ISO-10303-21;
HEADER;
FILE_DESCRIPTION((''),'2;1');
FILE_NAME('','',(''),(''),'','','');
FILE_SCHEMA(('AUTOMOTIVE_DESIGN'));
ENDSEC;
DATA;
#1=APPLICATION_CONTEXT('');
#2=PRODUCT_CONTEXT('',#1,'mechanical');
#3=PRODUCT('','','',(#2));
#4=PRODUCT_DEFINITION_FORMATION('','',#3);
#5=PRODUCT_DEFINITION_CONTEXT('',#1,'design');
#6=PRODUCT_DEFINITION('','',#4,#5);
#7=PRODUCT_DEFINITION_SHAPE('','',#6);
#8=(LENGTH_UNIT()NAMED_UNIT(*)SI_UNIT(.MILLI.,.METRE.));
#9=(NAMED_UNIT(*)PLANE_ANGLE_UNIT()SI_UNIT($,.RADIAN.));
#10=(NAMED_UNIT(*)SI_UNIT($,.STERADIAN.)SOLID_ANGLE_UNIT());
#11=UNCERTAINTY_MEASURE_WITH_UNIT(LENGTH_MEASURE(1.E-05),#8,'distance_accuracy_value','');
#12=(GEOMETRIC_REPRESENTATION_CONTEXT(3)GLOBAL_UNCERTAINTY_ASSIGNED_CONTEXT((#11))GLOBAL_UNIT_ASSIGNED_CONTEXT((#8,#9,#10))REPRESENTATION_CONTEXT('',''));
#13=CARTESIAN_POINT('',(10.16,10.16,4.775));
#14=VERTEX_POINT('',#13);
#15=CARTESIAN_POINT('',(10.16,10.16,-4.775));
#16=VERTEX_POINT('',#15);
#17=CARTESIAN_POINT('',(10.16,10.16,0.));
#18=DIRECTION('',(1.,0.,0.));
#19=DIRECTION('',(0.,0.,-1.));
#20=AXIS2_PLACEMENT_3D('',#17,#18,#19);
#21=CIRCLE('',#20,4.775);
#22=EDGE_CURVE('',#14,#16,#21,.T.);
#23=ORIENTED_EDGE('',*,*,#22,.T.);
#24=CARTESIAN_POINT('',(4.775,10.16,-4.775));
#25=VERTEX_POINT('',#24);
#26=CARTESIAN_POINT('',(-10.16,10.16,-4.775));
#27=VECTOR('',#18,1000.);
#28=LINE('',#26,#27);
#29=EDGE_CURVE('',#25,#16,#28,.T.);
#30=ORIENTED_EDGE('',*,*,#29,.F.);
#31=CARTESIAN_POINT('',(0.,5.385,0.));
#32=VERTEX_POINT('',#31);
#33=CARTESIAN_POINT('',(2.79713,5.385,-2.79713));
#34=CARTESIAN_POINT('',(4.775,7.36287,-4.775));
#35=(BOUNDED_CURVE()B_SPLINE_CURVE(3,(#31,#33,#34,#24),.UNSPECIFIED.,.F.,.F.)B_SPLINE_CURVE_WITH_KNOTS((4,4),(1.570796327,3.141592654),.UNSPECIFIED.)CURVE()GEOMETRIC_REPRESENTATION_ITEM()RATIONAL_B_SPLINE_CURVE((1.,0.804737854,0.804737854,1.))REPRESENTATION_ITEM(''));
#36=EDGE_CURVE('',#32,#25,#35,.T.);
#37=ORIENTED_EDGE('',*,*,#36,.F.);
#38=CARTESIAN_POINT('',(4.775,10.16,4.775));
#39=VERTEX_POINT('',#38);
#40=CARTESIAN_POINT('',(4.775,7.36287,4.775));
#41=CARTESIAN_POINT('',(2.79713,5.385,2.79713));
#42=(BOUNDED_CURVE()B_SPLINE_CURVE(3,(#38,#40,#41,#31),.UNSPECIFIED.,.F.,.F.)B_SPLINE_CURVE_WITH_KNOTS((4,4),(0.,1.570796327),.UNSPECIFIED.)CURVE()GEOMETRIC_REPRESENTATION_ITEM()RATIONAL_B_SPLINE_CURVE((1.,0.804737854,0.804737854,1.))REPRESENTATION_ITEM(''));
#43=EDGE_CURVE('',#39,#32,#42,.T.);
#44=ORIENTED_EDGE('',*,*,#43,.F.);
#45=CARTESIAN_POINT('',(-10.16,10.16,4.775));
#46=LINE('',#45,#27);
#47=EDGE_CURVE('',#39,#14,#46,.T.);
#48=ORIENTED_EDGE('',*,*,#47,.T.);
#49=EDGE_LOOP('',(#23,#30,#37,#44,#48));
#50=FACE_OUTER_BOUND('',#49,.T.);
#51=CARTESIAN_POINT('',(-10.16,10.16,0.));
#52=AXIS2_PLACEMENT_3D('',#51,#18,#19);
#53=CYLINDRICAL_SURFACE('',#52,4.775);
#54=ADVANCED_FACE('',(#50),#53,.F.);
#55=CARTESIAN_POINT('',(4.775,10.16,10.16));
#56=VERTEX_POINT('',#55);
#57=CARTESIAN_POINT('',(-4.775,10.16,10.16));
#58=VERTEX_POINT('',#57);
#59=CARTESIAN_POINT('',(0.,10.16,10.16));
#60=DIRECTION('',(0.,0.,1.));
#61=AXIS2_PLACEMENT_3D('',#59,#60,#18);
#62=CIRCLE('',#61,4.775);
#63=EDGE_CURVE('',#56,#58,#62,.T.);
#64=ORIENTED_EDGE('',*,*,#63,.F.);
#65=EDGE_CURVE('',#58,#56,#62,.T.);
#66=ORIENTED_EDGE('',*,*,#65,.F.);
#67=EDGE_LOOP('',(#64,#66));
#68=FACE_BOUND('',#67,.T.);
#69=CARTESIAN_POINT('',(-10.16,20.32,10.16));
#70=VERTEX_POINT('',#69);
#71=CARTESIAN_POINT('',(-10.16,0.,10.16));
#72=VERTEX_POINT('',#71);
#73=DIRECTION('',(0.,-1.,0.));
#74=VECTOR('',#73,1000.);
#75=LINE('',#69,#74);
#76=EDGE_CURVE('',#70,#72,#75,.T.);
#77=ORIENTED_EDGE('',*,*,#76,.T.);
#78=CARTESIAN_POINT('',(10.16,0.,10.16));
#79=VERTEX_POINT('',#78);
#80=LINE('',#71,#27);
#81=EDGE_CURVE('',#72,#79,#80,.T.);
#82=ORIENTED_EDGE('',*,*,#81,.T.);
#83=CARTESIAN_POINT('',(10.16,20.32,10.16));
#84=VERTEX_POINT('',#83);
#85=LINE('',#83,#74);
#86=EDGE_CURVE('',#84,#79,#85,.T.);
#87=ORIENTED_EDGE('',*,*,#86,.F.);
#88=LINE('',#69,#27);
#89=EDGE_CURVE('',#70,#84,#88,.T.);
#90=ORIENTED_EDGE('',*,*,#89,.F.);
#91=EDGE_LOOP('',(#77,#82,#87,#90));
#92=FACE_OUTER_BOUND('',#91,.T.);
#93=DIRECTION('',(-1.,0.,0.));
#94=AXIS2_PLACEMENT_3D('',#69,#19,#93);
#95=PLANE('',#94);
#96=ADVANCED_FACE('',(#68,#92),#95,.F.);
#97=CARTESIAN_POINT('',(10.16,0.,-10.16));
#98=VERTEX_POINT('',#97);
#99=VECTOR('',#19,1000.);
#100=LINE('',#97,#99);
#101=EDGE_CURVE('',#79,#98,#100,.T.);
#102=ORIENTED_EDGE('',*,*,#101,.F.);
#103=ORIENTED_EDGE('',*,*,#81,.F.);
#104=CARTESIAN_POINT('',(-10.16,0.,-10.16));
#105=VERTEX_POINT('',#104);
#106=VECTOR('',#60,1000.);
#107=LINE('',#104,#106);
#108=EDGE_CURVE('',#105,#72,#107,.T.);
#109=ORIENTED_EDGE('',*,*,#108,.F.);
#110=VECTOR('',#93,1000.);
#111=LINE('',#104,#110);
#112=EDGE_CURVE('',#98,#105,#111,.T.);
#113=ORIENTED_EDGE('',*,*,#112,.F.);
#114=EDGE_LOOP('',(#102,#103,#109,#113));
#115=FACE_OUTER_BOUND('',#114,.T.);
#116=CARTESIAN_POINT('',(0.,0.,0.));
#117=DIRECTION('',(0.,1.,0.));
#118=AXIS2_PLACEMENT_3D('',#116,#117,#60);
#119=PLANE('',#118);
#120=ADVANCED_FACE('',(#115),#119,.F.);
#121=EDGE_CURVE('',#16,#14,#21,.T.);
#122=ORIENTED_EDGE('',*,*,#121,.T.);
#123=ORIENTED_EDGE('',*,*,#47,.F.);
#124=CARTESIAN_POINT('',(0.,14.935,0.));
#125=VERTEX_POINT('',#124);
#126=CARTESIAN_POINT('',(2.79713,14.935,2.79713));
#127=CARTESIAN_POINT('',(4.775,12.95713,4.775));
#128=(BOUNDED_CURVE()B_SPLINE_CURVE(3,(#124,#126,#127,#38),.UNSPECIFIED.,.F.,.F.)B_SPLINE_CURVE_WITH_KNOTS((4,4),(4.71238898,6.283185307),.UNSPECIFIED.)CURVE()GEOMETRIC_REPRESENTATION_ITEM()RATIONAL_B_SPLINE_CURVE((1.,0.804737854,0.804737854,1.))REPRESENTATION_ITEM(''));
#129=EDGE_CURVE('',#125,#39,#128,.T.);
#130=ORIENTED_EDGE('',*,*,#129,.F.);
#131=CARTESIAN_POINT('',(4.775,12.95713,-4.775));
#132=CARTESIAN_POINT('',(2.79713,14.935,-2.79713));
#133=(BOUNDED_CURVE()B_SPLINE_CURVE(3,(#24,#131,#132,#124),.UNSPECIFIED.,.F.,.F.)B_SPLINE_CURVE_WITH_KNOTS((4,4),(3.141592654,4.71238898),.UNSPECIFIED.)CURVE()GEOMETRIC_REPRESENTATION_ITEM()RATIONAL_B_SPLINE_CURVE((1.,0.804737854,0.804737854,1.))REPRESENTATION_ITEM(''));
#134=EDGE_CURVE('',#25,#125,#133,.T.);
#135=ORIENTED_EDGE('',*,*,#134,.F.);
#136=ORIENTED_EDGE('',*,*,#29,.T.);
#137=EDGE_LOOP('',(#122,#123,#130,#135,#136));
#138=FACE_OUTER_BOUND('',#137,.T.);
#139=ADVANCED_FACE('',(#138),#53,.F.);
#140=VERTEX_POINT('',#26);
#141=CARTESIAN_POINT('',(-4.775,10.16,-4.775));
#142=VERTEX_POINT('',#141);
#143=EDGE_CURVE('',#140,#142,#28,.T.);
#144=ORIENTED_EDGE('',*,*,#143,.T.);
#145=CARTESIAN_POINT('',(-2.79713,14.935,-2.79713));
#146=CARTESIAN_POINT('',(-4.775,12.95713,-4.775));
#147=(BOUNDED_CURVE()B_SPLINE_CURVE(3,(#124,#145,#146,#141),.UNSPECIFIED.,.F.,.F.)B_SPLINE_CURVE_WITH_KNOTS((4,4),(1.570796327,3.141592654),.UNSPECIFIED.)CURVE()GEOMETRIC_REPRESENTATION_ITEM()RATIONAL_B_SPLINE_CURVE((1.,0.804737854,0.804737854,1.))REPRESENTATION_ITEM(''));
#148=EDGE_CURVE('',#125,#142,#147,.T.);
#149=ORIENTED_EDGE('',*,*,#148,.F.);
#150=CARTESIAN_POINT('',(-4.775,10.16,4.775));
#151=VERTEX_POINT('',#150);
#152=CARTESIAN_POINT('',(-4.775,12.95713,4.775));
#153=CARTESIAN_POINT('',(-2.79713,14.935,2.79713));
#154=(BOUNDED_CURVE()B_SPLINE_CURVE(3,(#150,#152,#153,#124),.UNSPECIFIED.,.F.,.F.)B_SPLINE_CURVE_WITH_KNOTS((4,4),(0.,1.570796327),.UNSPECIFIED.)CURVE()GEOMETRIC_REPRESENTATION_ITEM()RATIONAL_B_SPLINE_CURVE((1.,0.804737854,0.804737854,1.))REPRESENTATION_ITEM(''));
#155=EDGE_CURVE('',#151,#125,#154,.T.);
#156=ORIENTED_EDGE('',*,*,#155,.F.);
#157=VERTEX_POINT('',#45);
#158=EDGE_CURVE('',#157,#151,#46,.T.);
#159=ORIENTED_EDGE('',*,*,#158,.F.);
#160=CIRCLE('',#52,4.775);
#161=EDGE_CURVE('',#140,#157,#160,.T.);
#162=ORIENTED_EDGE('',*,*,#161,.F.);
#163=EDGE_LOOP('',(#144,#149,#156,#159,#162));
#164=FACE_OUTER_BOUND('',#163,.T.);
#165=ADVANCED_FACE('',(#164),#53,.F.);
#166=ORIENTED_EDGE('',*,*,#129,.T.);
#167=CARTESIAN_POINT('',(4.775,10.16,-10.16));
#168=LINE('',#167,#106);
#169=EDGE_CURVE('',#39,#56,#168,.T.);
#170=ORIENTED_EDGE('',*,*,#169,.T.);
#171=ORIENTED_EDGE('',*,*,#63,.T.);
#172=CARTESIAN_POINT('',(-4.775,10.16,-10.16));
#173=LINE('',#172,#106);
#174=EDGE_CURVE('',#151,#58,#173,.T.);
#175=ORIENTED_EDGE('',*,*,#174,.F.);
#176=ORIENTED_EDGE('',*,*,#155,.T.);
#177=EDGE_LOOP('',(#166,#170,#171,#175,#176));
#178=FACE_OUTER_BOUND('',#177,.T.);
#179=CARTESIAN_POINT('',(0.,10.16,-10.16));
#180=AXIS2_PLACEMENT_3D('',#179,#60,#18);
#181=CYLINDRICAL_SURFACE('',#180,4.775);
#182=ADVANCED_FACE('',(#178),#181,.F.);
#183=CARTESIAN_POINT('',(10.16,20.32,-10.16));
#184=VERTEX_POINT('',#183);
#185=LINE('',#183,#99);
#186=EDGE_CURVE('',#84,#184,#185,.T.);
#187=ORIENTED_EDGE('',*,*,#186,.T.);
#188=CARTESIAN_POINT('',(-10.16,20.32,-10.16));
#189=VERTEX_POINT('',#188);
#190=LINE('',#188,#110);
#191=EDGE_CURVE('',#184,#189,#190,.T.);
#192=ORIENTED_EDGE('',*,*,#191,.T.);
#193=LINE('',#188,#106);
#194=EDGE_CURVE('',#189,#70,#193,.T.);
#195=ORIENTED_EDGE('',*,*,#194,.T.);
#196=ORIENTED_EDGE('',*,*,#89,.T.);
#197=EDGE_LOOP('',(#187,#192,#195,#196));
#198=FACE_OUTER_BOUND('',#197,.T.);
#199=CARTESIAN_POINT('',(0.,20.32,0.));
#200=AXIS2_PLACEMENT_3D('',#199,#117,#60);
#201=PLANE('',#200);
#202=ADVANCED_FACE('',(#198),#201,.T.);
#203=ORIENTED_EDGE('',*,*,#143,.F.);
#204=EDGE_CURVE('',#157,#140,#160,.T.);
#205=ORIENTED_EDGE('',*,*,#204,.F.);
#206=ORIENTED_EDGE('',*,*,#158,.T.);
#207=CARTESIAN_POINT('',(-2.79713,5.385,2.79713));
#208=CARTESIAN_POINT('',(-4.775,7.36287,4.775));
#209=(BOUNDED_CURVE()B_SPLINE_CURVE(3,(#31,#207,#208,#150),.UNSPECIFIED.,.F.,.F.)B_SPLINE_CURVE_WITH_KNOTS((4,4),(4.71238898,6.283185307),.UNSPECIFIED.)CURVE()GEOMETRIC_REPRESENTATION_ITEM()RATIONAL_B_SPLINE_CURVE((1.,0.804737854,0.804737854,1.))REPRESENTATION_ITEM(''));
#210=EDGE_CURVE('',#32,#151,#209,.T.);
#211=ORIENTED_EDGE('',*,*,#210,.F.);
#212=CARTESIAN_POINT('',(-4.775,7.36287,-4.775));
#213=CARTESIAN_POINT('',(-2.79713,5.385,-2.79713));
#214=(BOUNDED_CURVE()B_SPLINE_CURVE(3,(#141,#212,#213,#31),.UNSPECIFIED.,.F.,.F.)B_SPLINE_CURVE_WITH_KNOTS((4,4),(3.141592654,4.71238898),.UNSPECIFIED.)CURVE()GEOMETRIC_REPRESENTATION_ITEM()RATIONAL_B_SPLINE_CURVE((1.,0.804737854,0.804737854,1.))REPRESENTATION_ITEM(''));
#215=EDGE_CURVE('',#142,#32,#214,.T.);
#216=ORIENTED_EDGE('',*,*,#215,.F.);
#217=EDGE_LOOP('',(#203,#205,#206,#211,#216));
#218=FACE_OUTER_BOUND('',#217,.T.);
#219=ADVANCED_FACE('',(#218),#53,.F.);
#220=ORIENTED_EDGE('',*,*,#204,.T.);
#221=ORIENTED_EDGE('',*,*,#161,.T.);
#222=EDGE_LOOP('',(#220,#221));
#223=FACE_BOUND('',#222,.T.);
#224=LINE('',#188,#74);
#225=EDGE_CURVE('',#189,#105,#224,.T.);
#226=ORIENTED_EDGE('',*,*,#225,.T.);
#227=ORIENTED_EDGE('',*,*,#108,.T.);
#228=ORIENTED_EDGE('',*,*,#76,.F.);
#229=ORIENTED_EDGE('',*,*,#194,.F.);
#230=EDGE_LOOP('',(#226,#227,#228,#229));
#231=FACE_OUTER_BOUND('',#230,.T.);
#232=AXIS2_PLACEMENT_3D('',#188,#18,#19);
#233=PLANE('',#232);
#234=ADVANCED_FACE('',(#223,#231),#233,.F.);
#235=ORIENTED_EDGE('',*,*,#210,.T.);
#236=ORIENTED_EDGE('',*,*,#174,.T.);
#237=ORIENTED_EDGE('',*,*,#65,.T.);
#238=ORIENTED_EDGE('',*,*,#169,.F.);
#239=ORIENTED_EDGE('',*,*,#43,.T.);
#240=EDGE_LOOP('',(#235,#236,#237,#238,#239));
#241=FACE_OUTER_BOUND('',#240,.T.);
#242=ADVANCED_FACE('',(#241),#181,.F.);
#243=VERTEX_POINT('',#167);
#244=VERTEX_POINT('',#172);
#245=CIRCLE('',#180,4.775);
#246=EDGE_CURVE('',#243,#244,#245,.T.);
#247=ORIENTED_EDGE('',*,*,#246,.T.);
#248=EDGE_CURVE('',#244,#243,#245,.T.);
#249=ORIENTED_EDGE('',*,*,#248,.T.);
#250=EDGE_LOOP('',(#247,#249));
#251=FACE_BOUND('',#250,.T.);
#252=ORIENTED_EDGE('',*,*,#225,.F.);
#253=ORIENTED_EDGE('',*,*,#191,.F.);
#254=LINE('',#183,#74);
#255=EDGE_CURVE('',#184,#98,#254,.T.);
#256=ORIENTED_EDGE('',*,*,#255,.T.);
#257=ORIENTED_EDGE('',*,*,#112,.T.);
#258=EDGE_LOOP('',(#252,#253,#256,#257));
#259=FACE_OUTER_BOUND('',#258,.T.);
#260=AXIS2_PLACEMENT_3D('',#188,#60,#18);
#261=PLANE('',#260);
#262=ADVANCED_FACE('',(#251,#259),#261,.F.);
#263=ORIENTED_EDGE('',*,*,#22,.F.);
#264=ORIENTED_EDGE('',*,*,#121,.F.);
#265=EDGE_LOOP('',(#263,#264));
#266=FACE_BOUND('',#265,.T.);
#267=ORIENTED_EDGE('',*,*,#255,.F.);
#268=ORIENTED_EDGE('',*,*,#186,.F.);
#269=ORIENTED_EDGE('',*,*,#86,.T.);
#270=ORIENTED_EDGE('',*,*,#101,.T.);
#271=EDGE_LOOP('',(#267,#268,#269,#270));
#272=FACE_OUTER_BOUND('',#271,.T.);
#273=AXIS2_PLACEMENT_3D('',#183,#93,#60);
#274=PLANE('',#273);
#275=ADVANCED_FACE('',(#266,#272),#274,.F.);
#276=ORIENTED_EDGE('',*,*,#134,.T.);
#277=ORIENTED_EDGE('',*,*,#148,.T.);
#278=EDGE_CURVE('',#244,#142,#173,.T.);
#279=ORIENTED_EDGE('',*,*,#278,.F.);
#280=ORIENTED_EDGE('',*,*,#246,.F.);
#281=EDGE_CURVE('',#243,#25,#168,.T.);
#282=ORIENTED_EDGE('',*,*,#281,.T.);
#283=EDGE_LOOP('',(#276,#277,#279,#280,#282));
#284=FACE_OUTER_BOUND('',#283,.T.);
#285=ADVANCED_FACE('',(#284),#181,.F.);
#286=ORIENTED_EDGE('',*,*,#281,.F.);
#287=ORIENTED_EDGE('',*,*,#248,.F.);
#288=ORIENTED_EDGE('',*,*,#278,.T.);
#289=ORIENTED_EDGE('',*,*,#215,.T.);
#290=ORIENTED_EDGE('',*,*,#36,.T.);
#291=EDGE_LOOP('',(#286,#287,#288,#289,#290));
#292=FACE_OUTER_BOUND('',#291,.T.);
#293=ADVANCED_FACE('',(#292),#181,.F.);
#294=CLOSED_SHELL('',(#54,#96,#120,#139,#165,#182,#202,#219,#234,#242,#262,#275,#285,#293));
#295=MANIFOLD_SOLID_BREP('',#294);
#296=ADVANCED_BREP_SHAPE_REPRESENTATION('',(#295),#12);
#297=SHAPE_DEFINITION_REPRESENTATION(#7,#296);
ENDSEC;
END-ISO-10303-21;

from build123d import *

# Parameters (mm, degrees)
BLOCK_PROFILE_20_32_SQUARE_W = 20.32
BLOCK_PROFILE_20_32_SQUARE_H = 20.32
CUBE_BLOCK_20_32_DEPTH       = 20.32
CROSS_HOLE_A_PROFILE_R       = 4.775
CROSS_HOLE_A_9_35_DEPTH      = 31.48
CROSS_HOLE_B_PROFILE_R       = 4.775
CROSS_HOLE_B_9_35_DEPTH      = 31.48


with BuildPart() as part:
    # Block Profile 20.32 Square → Cube Block 20.32 (new body)
    with BuildSketch(Plane(origin=(0, 0, 0), x_dir=(1, 0, 0), z_dir=(0, 1, 0))):
        Rectangle(BLOCK_PROFILE_20_32_SQUARE_W, BLOCK_PROFILE_20_32_SQUARE_H)
    extrude(amount=CUBE_BLOCK_20_32_DEPTH)

    # Cross Hole A Profile → Cross Hole A Ø9.35 (cut, through all)
    with BuildSketch(Plane.XY.offset(10.16)):
        with Locations((0, 10.16)):
            Circle(CROSS_HOLE_A_PROFILE_R)
    extrude(amount=-CROSS_HOLE_A_9_35_DEPTH, mode=Mode.SUBTRACT)

    # Cross Hole B Profile → Cross Hole B Ø9.35 (cut, through all)
    with BuildSketch(Plane(origin=(10.16, 0, 0), x_dir=(0, 0, -1), z_dir=(1, 0, 0))):
        with Locations((0, 10.16)):
            Circle(CROSS_HOLE_B_PROFILE_R)
    extrude(amount=-CROSS_HOLE_B_9_35_DEPTH, mode=Mode.SUBTRACT)


solid = part.part
